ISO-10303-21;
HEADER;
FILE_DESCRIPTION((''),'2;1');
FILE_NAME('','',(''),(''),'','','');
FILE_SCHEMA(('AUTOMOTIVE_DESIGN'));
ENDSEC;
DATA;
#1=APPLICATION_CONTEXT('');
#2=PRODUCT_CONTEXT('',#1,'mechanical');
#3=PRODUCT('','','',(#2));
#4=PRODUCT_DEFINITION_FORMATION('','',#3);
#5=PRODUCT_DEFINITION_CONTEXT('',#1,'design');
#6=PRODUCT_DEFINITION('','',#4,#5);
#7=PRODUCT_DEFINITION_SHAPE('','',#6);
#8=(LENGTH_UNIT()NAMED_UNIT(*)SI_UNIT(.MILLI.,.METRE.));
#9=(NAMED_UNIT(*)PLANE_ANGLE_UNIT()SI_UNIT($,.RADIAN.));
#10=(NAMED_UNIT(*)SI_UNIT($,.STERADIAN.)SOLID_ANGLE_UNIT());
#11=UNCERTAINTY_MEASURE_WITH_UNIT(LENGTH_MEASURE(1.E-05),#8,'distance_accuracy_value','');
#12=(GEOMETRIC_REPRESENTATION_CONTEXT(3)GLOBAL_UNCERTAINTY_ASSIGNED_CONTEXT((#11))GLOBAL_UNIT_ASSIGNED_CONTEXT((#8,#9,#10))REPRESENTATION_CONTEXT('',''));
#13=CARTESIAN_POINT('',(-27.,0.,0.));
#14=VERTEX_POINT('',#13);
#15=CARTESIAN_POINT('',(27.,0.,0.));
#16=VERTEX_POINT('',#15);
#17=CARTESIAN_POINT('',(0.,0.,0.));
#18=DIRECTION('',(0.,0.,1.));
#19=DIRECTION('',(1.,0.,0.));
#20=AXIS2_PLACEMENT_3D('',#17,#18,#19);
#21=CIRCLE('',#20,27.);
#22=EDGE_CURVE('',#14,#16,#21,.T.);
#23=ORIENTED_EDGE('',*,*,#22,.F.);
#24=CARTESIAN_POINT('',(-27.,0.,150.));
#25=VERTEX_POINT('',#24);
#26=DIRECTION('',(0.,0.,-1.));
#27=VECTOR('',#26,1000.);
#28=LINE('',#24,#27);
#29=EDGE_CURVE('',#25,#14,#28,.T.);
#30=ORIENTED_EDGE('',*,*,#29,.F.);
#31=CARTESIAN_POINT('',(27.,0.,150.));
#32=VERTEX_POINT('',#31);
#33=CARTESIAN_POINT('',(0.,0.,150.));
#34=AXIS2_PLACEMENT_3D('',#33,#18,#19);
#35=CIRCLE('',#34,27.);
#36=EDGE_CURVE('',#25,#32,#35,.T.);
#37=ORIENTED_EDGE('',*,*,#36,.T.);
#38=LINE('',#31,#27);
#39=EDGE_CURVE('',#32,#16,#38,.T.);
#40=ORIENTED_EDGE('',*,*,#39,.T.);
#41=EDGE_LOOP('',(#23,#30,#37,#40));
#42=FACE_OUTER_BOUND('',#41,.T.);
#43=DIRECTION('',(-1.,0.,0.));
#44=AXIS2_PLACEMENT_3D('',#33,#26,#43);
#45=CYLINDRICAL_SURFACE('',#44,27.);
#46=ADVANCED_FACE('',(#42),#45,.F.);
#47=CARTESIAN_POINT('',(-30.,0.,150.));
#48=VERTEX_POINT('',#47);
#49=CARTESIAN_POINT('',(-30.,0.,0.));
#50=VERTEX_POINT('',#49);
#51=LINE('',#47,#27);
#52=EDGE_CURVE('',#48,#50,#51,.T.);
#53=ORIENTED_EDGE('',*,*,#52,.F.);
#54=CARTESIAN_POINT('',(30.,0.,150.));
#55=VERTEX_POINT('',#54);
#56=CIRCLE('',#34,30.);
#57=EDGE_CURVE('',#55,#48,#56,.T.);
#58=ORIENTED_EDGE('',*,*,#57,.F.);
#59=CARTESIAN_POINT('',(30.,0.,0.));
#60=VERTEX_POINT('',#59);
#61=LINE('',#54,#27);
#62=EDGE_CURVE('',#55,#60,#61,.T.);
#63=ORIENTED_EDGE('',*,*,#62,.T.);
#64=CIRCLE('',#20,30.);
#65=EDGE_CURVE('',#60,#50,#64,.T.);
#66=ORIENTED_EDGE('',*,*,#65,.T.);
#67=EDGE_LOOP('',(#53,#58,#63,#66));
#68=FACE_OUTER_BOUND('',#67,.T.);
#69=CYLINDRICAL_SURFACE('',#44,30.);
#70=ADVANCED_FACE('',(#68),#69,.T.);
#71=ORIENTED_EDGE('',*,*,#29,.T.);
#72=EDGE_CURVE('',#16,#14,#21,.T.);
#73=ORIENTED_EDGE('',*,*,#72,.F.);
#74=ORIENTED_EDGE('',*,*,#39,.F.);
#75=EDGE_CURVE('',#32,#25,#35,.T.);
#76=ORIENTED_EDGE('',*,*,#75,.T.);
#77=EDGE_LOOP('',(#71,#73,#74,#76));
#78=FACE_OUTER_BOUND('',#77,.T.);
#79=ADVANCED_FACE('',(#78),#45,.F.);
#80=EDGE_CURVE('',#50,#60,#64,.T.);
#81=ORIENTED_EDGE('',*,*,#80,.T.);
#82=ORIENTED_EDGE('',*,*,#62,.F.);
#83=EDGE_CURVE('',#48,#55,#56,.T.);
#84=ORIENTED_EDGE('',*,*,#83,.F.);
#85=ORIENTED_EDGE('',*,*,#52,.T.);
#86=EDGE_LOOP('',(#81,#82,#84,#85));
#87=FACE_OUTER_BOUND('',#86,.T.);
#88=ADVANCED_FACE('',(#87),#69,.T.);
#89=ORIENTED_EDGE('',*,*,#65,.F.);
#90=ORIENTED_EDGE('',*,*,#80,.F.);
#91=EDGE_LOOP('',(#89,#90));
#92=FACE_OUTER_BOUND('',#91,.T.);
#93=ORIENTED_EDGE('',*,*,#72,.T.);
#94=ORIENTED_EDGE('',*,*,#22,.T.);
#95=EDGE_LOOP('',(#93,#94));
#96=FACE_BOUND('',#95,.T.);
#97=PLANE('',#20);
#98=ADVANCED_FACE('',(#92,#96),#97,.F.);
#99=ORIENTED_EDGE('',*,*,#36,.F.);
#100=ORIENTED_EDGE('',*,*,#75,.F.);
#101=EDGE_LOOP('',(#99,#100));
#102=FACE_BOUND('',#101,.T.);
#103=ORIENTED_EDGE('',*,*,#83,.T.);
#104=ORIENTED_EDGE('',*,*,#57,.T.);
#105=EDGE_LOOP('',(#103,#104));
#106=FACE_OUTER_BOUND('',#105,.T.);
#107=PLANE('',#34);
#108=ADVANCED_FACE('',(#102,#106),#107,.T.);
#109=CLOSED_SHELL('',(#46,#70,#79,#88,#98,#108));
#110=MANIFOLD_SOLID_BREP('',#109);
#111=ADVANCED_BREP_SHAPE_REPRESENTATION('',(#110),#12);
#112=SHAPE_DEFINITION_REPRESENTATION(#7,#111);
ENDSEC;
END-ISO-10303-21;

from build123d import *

# Parameters (mm, degrees)
SKETCH1_R           = 30
SKETCH1_R_2         = 27
BOSS_EXTRUDE1_DEPTH = 150


with BuildPart() as part:
    # Sketch1 → Boss-Extrude1 (new body)
    with BuildSketch(Plane.XY):
        Circle(SKETCH1_R)
        Circle(SKETCH1_R_2, mode=Mode.SUBTRACT)
    extrude(amount=BOSS_EXTRUDE1_DEPTH)


solid = part.part
